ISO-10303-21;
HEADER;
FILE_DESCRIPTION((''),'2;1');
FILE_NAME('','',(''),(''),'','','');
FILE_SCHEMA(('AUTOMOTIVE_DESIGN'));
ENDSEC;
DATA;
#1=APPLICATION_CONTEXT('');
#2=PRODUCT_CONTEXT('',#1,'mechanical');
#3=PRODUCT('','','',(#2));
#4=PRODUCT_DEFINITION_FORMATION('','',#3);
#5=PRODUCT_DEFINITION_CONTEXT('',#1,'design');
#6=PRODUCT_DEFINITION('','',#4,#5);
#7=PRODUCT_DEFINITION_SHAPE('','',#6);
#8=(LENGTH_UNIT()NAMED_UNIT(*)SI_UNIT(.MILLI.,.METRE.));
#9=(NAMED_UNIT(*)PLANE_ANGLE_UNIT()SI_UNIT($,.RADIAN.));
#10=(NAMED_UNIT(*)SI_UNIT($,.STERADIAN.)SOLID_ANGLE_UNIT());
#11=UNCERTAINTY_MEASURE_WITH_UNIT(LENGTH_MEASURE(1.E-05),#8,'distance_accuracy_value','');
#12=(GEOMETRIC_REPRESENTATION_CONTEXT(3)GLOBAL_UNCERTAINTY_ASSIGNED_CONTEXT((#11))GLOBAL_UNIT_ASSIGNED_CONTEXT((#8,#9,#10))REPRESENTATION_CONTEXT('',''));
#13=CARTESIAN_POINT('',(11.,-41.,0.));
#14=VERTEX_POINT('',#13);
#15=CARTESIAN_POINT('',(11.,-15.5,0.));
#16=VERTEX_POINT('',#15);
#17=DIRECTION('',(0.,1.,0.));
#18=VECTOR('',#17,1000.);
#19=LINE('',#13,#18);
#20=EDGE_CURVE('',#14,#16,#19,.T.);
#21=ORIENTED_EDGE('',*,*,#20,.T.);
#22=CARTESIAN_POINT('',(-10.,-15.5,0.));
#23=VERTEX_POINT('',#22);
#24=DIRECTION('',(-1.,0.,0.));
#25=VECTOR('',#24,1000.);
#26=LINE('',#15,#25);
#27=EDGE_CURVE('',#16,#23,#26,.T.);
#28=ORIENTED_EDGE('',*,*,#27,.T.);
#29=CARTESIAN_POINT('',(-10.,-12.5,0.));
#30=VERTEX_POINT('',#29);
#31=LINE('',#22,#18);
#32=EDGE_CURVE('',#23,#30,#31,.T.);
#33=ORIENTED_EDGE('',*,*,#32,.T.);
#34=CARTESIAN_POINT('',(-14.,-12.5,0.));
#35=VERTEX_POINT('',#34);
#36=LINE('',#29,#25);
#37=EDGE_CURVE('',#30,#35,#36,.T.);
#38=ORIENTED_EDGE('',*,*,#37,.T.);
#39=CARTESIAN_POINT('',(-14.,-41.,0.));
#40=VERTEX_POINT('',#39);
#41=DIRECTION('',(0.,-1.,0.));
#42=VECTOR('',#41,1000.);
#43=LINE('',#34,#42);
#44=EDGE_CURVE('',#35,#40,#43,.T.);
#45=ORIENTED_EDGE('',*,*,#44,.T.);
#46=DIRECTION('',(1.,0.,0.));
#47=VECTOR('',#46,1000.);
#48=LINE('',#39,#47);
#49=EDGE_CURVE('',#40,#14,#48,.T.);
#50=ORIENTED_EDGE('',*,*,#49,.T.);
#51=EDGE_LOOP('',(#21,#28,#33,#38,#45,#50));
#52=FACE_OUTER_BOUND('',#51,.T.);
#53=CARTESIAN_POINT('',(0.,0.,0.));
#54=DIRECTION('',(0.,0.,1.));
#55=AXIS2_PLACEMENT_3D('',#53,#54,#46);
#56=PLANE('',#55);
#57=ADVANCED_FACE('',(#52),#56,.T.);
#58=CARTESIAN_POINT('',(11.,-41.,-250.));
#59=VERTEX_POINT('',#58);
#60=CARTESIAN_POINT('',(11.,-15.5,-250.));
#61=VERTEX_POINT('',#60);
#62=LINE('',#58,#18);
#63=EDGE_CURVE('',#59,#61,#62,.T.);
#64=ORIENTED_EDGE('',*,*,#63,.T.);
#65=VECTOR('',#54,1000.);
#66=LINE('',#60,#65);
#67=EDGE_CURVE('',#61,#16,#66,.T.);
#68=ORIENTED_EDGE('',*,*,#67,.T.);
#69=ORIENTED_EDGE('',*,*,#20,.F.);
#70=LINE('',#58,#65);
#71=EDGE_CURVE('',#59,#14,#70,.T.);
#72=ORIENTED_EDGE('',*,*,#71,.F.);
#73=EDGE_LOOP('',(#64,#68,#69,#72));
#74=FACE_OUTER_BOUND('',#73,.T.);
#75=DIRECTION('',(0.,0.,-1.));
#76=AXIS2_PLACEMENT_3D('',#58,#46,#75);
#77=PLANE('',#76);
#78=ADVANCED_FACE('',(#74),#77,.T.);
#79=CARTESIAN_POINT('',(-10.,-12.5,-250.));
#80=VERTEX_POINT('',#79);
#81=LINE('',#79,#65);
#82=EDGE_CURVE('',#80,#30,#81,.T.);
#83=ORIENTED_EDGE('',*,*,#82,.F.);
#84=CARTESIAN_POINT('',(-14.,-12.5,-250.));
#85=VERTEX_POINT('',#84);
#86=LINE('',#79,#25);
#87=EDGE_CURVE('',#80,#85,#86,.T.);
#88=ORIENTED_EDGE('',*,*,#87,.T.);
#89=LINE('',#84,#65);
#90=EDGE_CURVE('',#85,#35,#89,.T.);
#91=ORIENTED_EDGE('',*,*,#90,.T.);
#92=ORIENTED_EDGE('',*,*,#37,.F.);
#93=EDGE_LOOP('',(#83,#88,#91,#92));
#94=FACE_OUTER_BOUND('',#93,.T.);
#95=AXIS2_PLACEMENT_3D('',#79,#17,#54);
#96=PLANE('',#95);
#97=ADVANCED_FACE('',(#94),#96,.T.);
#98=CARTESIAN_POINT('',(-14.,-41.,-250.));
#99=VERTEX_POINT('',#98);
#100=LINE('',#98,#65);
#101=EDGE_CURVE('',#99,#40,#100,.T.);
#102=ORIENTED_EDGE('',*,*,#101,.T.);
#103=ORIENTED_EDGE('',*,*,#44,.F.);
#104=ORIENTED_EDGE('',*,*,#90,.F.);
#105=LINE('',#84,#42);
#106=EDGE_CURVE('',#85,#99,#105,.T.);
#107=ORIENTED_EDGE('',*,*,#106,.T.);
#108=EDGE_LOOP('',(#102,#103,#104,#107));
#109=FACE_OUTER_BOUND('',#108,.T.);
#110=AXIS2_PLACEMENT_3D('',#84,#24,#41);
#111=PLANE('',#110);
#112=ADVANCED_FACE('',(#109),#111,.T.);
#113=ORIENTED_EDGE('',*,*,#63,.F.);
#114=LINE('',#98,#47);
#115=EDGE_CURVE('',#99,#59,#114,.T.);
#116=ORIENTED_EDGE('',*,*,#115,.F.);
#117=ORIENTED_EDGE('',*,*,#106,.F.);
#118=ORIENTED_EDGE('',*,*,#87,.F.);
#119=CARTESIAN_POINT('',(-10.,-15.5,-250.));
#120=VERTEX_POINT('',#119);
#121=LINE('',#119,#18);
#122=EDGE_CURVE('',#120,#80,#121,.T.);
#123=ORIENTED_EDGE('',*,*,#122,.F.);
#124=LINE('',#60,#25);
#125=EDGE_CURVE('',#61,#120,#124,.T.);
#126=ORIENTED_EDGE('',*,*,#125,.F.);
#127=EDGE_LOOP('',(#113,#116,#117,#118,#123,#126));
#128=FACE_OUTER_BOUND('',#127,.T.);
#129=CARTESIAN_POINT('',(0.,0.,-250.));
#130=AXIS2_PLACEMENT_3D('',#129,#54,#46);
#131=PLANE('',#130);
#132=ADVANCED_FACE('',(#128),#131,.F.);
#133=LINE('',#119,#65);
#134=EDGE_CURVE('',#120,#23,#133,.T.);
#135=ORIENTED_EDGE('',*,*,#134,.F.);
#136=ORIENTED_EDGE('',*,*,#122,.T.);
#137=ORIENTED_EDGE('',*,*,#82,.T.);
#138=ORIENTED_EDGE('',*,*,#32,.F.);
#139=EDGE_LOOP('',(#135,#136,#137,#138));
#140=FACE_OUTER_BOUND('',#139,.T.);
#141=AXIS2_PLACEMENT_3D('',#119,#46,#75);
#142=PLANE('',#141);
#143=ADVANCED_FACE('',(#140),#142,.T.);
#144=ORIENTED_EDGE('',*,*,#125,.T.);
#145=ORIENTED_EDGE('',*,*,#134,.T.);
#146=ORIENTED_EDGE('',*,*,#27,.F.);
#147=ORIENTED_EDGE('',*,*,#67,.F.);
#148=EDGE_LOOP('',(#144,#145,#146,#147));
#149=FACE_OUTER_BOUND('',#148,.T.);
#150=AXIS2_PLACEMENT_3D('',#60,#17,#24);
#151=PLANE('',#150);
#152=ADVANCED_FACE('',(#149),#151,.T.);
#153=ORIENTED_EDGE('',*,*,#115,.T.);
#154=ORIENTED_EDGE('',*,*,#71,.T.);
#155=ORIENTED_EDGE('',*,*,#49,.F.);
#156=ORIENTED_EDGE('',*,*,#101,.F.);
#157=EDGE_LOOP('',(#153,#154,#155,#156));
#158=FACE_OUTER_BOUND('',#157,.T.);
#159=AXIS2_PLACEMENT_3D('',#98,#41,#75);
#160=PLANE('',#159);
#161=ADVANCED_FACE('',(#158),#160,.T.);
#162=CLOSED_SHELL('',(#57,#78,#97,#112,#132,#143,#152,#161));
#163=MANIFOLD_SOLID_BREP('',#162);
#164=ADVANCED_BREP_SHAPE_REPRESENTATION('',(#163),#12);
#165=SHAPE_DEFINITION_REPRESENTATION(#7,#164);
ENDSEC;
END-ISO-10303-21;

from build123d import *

# Parameters (mm, degrees)
EXTRUDE_1_DEPTH = 250


with BuildPart() as part:
    # 草图1 → 凸台-拉伸1 (new body)
    with BuildSketch(Plane.XY):
        Polygon((-10, -12.5), (-14, -12.5), (-14, -41), (11, -41), (11, -15.5), (-10, -15.5), align=None)
    extrude(amount=-EXTRUDE_1_DEPTH)


solid = part.part
